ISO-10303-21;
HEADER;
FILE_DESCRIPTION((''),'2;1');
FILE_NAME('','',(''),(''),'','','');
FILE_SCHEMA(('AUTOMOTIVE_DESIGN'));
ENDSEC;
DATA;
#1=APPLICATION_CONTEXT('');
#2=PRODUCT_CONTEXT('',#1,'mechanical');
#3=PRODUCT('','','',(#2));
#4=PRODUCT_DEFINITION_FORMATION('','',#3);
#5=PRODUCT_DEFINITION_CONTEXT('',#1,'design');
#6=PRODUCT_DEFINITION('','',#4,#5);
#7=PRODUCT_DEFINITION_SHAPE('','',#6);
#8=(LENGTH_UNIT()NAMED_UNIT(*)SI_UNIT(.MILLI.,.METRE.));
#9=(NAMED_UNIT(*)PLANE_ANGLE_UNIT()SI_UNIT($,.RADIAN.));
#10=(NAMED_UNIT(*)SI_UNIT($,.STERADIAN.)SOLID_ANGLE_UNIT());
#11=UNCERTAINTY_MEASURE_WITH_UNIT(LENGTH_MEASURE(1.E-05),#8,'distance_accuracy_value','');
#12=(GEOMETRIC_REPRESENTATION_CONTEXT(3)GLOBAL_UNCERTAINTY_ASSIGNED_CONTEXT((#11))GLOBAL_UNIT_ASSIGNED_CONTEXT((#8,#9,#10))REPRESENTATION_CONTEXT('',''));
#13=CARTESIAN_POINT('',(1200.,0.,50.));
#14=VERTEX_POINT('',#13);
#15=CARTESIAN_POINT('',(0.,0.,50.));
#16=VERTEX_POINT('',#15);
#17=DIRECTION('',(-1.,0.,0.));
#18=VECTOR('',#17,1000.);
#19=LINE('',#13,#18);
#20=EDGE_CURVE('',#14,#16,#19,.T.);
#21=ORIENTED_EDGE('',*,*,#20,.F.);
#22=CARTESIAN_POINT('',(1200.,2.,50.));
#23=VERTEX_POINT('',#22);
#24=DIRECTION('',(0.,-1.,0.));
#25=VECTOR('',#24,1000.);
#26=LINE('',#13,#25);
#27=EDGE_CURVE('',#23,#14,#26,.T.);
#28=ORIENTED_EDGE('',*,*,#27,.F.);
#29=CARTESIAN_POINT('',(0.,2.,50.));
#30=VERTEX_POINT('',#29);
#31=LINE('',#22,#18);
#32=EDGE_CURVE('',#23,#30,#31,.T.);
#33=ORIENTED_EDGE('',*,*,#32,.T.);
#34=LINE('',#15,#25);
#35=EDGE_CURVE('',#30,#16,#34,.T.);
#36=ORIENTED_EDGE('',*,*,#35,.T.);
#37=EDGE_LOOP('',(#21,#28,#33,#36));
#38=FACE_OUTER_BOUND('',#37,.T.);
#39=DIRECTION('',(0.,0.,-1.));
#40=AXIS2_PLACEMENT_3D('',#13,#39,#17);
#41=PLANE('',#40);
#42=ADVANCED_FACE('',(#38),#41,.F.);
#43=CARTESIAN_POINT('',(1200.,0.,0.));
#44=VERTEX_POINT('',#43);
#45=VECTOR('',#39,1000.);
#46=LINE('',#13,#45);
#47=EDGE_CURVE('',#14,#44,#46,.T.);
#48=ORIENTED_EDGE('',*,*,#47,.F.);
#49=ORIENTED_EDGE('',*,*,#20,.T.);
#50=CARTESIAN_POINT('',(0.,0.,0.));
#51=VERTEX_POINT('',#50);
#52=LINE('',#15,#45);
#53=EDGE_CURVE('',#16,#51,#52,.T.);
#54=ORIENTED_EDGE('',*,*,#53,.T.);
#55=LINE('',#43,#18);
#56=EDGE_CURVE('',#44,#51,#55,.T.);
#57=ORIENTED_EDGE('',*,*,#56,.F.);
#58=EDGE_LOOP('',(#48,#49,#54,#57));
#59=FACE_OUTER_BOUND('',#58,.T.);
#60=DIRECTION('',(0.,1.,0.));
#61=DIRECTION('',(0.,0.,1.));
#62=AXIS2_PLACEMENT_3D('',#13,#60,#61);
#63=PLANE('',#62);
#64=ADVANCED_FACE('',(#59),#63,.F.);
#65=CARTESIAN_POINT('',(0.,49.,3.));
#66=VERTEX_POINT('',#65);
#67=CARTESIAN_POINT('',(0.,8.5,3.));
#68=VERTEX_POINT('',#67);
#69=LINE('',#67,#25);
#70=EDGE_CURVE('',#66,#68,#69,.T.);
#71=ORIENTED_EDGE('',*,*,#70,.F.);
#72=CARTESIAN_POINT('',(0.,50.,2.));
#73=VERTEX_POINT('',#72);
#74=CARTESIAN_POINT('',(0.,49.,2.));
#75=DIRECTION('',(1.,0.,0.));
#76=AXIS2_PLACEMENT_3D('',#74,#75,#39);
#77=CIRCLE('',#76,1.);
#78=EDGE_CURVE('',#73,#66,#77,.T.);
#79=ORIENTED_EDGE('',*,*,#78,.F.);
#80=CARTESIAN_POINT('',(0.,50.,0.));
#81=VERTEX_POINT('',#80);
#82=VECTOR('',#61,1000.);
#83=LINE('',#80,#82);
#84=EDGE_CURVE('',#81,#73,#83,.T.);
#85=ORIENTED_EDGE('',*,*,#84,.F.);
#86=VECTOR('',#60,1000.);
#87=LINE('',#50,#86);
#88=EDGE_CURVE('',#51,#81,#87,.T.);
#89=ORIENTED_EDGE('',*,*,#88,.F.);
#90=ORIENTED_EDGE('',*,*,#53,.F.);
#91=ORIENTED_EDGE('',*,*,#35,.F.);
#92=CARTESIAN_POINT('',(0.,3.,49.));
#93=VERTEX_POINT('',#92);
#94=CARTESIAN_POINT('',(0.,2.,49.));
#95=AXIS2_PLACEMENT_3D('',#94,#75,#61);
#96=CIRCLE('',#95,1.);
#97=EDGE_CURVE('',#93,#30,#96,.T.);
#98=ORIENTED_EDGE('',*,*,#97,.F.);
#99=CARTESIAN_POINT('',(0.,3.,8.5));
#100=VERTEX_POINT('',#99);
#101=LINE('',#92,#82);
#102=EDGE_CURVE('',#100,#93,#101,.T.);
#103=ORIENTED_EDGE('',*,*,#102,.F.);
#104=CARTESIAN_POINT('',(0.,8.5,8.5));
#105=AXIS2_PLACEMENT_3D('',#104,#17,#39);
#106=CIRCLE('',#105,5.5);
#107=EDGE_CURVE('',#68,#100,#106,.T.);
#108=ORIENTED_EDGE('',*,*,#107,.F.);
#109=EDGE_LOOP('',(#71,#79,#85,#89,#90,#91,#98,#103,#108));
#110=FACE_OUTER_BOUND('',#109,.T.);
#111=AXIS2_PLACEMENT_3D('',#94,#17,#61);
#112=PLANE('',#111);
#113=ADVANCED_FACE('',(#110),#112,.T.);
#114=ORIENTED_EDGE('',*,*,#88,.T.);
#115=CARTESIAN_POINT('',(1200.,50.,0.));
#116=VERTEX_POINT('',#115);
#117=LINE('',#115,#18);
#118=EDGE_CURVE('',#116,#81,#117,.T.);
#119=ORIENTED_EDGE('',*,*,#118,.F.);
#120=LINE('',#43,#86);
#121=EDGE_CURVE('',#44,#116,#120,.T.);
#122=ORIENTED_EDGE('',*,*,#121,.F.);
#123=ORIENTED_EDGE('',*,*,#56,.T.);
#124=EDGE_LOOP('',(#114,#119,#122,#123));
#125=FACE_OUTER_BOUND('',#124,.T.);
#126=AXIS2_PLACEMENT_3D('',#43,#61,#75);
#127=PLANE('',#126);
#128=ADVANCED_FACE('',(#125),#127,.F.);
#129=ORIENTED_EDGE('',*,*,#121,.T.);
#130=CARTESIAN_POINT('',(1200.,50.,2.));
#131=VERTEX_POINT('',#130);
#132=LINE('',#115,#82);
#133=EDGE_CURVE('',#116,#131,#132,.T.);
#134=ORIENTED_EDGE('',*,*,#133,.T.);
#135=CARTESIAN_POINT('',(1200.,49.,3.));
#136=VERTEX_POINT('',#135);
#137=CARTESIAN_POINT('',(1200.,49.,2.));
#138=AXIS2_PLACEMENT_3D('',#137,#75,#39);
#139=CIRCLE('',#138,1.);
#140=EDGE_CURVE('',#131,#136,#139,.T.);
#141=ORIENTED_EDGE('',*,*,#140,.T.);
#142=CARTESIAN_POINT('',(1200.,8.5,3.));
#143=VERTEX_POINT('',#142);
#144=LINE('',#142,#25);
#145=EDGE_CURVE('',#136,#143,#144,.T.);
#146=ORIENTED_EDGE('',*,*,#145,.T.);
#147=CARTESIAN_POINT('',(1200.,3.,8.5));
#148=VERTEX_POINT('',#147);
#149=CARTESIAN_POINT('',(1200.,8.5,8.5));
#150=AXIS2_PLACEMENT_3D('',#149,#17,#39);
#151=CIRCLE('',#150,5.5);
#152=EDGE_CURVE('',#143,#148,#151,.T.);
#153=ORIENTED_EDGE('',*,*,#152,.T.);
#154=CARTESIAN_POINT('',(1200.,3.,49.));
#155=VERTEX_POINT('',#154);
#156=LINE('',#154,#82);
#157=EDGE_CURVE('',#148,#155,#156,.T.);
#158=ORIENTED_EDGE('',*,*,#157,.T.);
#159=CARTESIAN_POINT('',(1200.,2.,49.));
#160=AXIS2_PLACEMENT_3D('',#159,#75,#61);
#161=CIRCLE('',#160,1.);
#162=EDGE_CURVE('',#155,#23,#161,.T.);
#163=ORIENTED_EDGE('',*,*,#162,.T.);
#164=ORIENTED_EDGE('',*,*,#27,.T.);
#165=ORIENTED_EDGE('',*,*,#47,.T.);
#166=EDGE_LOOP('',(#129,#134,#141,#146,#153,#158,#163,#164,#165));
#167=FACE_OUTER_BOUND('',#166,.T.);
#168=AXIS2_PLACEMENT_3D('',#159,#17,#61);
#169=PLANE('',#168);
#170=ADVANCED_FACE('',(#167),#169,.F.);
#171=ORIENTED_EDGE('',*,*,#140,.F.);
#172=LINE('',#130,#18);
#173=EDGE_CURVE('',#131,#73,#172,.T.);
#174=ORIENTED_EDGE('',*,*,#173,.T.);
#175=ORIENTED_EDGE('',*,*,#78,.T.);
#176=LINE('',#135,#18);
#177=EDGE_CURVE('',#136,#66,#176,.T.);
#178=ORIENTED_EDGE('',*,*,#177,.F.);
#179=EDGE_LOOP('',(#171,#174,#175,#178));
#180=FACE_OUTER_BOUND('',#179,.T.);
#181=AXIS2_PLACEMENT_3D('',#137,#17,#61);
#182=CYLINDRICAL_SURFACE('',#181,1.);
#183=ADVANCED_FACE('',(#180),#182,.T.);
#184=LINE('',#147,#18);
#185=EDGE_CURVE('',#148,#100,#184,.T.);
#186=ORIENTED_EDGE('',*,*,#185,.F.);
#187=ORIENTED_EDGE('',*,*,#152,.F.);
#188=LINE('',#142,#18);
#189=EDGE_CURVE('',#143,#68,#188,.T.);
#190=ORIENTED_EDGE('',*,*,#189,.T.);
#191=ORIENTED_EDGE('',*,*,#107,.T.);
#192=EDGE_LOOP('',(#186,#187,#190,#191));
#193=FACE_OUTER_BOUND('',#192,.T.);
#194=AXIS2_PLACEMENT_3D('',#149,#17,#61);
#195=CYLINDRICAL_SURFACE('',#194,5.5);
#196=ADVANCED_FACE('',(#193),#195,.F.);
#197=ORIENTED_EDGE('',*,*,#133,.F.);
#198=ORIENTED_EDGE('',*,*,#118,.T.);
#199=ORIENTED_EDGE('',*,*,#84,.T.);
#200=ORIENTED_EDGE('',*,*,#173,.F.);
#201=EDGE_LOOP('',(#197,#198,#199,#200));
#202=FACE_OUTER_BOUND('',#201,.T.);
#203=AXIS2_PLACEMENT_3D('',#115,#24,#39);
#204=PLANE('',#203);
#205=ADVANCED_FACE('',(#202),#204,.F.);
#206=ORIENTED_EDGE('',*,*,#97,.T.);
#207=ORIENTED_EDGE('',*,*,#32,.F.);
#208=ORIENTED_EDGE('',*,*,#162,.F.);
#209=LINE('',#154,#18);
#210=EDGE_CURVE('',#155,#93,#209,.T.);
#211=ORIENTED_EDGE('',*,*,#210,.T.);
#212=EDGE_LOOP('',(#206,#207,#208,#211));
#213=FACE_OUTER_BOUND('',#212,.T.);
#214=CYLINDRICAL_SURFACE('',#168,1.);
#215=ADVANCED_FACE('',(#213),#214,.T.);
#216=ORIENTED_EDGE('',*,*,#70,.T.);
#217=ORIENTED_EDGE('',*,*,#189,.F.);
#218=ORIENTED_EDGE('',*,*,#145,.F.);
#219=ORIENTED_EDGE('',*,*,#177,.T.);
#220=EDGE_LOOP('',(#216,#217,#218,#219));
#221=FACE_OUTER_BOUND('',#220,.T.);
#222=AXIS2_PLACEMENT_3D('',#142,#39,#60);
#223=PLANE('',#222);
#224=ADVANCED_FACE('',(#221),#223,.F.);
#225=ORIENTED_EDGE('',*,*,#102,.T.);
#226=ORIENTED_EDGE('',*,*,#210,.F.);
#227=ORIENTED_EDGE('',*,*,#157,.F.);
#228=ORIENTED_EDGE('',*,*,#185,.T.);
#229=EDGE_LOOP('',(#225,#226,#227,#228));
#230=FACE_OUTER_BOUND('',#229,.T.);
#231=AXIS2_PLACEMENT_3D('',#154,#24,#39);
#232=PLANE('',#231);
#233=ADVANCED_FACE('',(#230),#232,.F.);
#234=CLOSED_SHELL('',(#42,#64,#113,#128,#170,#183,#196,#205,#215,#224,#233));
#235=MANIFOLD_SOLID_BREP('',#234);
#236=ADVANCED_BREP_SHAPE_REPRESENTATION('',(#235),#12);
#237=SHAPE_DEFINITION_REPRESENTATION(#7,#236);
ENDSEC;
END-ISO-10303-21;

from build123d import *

# Parameters (mm, degrees)
BASE_DEPTH = 1200


with BuildPart() as part:
    # Sketch1 → Base (new body)
    with BuildSketch(Plane.YZ):
        with BuildLine():
            Line((0, 50), (0, 0))
            Line((0, 0), (50, 0))
            Line((50, 0), (50, 2))
            ThreePointArc((50, 2), (49.707106781, 2.707106781), (49, 3))
            Line((49, 3), (8.5, 3))
            ThreePointArc((8.5, 3), (4.610912703, 4.610912703), (3, 8.5))
            Line((3, 8.5), (3, 49))
            ThreePointArc((3, 49), (2.707106781, 49.707106781), (2, 50))
            Line((2, 50), (0, 50))
        make_face()
    extrude(amount=BASE_DEPTH)


solid = part.part
